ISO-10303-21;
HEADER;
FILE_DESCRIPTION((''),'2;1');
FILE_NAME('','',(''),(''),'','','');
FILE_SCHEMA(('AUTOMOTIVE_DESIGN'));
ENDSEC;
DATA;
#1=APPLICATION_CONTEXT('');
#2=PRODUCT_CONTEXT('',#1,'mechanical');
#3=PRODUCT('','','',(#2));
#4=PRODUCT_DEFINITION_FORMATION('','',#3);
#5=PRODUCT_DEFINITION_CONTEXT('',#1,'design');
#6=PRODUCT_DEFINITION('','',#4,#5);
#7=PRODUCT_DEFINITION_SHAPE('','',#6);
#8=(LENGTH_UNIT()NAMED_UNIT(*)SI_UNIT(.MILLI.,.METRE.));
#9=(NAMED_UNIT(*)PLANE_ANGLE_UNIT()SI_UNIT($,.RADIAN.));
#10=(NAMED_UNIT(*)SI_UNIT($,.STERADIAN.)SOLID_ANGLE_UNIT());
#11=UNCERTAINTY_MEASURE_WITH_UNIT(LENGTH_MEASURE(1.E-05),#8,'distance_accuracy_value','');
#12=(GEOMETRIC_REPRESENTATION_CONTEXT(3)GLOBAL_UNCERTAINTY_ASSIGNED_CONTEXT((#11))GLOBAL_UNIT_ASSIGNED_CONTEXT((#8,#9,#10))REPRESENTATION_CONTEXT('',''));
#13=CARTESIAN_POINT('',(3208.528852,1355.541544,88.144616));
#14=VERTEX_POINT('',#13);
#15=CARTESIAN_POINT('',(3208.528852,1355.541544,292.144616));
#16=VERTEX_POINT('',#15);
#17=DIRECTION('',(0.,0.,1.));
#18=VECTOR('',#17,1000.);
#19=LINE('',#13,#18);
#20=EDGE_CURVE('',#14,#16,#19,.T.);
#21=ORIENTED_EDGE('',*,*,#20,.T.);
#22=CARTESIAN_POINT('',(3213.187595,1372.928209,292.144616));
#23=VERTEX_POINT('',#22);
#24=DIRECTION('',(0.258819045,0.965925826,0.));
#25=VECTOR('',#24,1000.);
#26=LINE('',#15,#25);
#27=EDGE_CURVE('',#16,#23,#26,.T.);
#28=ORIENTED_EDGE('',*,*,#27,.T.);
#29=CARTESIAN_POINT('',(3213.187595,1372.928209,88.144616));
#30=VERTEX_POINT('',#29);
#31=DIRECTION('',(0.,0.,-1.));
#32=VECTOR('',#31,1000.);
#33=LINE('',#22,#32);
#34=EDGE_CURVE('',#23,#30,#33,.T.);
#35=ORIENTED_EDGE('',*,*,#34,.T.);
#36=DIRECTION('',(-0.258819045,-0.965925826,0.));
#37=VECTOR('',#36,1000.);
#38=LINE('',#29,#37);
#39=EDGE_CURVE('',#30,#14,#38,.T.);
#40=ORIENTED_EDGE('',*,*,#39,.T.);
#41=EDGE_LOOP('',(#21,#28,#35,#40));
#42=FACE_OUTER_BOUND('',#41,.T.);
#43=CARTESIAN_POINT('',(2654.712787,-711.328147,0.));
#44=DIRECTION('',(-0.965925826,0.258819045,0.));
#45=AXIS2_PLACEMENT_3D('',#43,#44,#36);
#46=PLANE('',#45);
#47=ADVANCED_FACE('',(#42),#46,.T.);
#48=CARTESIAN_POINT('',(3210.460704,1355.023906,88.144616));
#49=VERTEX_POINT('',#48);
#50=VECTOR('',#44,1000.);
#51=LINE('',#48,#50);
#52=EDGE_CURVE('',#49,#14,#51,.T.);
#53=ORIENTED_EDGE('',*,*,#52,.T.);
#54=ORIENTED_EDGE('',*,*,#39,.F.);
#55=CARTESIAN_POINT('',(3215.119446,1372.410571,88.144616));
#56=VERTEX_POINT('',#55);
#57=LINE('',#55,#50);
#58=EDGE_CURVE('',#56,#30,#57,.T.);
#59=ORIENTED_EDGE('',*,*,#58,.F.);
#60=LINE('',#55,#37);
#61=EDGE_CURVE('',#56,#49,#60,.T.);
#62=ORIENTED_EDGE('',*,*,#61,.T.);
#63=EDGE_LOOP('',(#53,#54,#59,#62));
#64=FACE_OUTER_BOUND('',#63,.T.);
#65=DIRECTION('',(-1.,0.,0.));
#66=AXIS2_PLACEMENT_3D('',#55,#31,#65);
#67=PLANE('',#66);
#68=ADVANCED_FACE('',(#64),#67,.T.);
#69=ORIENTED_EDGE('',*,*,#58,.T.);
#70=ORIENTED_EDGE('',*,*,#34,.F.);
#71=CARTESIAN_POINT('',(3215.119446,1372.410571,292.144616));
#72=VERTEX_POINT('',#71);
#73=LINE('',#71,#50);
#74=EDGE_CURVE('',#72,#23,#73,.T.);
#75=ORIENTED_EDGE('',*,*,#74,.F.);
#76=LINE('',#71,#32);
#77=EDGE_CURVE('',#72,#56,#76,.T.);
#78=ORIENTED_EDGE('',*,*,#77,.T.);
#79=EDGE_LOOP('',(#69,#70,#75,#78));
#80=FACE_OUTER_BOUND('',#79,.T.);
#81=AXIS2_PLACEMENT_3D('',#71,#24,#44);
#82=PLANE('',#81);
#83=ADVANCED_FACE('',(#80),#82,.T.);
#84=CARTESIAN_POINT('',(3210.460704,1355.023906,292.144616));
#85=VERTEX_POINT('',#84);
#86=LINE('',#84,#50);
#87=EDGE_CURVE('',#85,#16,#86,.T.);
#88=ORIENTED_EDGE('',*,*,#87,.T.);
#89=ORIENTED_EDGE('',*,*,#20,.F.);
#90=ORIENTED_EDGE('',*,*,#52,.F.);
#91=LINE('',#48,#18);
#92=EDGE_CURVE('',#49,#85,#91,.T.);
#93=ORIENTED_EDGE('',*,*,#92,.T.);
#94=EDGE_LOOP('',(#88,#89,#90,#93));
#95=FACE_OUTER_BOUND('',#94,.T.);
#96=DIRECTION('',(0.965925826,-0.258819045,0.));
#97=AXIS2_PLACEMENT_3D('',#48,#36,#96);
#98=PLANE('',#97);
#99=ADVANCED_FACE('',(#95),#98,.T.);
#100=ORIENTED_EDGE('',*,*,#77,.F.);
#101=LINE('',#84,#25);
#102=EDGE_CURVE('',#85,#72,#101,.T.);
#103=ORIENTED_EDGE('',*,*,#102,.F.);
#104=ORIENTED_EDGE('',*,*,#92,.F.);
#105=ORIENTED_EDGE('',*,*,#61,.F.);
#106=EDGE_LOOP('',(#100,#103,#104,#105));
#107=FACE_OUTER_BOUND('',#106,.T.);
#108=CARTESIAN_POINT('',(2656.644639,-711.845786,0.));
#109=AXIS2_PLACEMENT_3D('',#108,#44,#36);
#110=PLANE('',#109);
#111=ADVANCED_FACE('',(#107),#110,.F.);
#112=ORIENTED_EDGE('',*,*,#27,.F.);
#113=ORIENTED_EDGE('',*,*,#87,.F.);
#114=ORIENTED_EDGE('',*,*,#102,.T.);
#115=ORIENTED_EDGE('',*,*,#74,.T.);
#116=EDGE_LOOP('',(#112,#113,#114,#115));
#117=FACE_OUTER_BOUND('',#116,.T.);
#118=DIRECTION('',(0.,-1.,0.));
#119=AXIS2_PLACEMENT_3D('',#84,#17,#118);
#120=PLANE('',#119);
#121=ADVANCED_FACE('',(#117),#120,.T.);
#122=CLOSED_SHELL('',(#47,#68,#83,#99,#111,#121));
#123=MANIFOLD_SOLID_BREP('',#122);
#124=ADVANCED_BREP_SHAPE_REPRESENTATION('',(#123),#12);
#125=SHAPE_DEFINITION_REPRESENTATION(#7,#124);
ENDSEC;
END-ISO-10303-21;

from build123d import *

# Parameters (mm, degrees)
SKETCH_1_W      = 18
SKETCH_1_H      = 204
EXTRUDE_1_DEPTH = 2


with BuildPart() as part:
    # 草图1 → 凸台-拉伸1 (new body)
    with BuildSketch(Plane(origin=(2654.71278719, -711.328147464, 0), x_dir=(-0.25881904510251985, -0.9659258262890685, 0), z_dir=(-0.9659258262890685, 0.25881904510251985, 0))):
        with Locations((-2148.780959522, 190.144615796)):
            Rectangle(SKETCH_1_W, SKETCH_1_H)
    extrude(amount=-EXTRUDE_1_DEPTH)


solid = part.part
